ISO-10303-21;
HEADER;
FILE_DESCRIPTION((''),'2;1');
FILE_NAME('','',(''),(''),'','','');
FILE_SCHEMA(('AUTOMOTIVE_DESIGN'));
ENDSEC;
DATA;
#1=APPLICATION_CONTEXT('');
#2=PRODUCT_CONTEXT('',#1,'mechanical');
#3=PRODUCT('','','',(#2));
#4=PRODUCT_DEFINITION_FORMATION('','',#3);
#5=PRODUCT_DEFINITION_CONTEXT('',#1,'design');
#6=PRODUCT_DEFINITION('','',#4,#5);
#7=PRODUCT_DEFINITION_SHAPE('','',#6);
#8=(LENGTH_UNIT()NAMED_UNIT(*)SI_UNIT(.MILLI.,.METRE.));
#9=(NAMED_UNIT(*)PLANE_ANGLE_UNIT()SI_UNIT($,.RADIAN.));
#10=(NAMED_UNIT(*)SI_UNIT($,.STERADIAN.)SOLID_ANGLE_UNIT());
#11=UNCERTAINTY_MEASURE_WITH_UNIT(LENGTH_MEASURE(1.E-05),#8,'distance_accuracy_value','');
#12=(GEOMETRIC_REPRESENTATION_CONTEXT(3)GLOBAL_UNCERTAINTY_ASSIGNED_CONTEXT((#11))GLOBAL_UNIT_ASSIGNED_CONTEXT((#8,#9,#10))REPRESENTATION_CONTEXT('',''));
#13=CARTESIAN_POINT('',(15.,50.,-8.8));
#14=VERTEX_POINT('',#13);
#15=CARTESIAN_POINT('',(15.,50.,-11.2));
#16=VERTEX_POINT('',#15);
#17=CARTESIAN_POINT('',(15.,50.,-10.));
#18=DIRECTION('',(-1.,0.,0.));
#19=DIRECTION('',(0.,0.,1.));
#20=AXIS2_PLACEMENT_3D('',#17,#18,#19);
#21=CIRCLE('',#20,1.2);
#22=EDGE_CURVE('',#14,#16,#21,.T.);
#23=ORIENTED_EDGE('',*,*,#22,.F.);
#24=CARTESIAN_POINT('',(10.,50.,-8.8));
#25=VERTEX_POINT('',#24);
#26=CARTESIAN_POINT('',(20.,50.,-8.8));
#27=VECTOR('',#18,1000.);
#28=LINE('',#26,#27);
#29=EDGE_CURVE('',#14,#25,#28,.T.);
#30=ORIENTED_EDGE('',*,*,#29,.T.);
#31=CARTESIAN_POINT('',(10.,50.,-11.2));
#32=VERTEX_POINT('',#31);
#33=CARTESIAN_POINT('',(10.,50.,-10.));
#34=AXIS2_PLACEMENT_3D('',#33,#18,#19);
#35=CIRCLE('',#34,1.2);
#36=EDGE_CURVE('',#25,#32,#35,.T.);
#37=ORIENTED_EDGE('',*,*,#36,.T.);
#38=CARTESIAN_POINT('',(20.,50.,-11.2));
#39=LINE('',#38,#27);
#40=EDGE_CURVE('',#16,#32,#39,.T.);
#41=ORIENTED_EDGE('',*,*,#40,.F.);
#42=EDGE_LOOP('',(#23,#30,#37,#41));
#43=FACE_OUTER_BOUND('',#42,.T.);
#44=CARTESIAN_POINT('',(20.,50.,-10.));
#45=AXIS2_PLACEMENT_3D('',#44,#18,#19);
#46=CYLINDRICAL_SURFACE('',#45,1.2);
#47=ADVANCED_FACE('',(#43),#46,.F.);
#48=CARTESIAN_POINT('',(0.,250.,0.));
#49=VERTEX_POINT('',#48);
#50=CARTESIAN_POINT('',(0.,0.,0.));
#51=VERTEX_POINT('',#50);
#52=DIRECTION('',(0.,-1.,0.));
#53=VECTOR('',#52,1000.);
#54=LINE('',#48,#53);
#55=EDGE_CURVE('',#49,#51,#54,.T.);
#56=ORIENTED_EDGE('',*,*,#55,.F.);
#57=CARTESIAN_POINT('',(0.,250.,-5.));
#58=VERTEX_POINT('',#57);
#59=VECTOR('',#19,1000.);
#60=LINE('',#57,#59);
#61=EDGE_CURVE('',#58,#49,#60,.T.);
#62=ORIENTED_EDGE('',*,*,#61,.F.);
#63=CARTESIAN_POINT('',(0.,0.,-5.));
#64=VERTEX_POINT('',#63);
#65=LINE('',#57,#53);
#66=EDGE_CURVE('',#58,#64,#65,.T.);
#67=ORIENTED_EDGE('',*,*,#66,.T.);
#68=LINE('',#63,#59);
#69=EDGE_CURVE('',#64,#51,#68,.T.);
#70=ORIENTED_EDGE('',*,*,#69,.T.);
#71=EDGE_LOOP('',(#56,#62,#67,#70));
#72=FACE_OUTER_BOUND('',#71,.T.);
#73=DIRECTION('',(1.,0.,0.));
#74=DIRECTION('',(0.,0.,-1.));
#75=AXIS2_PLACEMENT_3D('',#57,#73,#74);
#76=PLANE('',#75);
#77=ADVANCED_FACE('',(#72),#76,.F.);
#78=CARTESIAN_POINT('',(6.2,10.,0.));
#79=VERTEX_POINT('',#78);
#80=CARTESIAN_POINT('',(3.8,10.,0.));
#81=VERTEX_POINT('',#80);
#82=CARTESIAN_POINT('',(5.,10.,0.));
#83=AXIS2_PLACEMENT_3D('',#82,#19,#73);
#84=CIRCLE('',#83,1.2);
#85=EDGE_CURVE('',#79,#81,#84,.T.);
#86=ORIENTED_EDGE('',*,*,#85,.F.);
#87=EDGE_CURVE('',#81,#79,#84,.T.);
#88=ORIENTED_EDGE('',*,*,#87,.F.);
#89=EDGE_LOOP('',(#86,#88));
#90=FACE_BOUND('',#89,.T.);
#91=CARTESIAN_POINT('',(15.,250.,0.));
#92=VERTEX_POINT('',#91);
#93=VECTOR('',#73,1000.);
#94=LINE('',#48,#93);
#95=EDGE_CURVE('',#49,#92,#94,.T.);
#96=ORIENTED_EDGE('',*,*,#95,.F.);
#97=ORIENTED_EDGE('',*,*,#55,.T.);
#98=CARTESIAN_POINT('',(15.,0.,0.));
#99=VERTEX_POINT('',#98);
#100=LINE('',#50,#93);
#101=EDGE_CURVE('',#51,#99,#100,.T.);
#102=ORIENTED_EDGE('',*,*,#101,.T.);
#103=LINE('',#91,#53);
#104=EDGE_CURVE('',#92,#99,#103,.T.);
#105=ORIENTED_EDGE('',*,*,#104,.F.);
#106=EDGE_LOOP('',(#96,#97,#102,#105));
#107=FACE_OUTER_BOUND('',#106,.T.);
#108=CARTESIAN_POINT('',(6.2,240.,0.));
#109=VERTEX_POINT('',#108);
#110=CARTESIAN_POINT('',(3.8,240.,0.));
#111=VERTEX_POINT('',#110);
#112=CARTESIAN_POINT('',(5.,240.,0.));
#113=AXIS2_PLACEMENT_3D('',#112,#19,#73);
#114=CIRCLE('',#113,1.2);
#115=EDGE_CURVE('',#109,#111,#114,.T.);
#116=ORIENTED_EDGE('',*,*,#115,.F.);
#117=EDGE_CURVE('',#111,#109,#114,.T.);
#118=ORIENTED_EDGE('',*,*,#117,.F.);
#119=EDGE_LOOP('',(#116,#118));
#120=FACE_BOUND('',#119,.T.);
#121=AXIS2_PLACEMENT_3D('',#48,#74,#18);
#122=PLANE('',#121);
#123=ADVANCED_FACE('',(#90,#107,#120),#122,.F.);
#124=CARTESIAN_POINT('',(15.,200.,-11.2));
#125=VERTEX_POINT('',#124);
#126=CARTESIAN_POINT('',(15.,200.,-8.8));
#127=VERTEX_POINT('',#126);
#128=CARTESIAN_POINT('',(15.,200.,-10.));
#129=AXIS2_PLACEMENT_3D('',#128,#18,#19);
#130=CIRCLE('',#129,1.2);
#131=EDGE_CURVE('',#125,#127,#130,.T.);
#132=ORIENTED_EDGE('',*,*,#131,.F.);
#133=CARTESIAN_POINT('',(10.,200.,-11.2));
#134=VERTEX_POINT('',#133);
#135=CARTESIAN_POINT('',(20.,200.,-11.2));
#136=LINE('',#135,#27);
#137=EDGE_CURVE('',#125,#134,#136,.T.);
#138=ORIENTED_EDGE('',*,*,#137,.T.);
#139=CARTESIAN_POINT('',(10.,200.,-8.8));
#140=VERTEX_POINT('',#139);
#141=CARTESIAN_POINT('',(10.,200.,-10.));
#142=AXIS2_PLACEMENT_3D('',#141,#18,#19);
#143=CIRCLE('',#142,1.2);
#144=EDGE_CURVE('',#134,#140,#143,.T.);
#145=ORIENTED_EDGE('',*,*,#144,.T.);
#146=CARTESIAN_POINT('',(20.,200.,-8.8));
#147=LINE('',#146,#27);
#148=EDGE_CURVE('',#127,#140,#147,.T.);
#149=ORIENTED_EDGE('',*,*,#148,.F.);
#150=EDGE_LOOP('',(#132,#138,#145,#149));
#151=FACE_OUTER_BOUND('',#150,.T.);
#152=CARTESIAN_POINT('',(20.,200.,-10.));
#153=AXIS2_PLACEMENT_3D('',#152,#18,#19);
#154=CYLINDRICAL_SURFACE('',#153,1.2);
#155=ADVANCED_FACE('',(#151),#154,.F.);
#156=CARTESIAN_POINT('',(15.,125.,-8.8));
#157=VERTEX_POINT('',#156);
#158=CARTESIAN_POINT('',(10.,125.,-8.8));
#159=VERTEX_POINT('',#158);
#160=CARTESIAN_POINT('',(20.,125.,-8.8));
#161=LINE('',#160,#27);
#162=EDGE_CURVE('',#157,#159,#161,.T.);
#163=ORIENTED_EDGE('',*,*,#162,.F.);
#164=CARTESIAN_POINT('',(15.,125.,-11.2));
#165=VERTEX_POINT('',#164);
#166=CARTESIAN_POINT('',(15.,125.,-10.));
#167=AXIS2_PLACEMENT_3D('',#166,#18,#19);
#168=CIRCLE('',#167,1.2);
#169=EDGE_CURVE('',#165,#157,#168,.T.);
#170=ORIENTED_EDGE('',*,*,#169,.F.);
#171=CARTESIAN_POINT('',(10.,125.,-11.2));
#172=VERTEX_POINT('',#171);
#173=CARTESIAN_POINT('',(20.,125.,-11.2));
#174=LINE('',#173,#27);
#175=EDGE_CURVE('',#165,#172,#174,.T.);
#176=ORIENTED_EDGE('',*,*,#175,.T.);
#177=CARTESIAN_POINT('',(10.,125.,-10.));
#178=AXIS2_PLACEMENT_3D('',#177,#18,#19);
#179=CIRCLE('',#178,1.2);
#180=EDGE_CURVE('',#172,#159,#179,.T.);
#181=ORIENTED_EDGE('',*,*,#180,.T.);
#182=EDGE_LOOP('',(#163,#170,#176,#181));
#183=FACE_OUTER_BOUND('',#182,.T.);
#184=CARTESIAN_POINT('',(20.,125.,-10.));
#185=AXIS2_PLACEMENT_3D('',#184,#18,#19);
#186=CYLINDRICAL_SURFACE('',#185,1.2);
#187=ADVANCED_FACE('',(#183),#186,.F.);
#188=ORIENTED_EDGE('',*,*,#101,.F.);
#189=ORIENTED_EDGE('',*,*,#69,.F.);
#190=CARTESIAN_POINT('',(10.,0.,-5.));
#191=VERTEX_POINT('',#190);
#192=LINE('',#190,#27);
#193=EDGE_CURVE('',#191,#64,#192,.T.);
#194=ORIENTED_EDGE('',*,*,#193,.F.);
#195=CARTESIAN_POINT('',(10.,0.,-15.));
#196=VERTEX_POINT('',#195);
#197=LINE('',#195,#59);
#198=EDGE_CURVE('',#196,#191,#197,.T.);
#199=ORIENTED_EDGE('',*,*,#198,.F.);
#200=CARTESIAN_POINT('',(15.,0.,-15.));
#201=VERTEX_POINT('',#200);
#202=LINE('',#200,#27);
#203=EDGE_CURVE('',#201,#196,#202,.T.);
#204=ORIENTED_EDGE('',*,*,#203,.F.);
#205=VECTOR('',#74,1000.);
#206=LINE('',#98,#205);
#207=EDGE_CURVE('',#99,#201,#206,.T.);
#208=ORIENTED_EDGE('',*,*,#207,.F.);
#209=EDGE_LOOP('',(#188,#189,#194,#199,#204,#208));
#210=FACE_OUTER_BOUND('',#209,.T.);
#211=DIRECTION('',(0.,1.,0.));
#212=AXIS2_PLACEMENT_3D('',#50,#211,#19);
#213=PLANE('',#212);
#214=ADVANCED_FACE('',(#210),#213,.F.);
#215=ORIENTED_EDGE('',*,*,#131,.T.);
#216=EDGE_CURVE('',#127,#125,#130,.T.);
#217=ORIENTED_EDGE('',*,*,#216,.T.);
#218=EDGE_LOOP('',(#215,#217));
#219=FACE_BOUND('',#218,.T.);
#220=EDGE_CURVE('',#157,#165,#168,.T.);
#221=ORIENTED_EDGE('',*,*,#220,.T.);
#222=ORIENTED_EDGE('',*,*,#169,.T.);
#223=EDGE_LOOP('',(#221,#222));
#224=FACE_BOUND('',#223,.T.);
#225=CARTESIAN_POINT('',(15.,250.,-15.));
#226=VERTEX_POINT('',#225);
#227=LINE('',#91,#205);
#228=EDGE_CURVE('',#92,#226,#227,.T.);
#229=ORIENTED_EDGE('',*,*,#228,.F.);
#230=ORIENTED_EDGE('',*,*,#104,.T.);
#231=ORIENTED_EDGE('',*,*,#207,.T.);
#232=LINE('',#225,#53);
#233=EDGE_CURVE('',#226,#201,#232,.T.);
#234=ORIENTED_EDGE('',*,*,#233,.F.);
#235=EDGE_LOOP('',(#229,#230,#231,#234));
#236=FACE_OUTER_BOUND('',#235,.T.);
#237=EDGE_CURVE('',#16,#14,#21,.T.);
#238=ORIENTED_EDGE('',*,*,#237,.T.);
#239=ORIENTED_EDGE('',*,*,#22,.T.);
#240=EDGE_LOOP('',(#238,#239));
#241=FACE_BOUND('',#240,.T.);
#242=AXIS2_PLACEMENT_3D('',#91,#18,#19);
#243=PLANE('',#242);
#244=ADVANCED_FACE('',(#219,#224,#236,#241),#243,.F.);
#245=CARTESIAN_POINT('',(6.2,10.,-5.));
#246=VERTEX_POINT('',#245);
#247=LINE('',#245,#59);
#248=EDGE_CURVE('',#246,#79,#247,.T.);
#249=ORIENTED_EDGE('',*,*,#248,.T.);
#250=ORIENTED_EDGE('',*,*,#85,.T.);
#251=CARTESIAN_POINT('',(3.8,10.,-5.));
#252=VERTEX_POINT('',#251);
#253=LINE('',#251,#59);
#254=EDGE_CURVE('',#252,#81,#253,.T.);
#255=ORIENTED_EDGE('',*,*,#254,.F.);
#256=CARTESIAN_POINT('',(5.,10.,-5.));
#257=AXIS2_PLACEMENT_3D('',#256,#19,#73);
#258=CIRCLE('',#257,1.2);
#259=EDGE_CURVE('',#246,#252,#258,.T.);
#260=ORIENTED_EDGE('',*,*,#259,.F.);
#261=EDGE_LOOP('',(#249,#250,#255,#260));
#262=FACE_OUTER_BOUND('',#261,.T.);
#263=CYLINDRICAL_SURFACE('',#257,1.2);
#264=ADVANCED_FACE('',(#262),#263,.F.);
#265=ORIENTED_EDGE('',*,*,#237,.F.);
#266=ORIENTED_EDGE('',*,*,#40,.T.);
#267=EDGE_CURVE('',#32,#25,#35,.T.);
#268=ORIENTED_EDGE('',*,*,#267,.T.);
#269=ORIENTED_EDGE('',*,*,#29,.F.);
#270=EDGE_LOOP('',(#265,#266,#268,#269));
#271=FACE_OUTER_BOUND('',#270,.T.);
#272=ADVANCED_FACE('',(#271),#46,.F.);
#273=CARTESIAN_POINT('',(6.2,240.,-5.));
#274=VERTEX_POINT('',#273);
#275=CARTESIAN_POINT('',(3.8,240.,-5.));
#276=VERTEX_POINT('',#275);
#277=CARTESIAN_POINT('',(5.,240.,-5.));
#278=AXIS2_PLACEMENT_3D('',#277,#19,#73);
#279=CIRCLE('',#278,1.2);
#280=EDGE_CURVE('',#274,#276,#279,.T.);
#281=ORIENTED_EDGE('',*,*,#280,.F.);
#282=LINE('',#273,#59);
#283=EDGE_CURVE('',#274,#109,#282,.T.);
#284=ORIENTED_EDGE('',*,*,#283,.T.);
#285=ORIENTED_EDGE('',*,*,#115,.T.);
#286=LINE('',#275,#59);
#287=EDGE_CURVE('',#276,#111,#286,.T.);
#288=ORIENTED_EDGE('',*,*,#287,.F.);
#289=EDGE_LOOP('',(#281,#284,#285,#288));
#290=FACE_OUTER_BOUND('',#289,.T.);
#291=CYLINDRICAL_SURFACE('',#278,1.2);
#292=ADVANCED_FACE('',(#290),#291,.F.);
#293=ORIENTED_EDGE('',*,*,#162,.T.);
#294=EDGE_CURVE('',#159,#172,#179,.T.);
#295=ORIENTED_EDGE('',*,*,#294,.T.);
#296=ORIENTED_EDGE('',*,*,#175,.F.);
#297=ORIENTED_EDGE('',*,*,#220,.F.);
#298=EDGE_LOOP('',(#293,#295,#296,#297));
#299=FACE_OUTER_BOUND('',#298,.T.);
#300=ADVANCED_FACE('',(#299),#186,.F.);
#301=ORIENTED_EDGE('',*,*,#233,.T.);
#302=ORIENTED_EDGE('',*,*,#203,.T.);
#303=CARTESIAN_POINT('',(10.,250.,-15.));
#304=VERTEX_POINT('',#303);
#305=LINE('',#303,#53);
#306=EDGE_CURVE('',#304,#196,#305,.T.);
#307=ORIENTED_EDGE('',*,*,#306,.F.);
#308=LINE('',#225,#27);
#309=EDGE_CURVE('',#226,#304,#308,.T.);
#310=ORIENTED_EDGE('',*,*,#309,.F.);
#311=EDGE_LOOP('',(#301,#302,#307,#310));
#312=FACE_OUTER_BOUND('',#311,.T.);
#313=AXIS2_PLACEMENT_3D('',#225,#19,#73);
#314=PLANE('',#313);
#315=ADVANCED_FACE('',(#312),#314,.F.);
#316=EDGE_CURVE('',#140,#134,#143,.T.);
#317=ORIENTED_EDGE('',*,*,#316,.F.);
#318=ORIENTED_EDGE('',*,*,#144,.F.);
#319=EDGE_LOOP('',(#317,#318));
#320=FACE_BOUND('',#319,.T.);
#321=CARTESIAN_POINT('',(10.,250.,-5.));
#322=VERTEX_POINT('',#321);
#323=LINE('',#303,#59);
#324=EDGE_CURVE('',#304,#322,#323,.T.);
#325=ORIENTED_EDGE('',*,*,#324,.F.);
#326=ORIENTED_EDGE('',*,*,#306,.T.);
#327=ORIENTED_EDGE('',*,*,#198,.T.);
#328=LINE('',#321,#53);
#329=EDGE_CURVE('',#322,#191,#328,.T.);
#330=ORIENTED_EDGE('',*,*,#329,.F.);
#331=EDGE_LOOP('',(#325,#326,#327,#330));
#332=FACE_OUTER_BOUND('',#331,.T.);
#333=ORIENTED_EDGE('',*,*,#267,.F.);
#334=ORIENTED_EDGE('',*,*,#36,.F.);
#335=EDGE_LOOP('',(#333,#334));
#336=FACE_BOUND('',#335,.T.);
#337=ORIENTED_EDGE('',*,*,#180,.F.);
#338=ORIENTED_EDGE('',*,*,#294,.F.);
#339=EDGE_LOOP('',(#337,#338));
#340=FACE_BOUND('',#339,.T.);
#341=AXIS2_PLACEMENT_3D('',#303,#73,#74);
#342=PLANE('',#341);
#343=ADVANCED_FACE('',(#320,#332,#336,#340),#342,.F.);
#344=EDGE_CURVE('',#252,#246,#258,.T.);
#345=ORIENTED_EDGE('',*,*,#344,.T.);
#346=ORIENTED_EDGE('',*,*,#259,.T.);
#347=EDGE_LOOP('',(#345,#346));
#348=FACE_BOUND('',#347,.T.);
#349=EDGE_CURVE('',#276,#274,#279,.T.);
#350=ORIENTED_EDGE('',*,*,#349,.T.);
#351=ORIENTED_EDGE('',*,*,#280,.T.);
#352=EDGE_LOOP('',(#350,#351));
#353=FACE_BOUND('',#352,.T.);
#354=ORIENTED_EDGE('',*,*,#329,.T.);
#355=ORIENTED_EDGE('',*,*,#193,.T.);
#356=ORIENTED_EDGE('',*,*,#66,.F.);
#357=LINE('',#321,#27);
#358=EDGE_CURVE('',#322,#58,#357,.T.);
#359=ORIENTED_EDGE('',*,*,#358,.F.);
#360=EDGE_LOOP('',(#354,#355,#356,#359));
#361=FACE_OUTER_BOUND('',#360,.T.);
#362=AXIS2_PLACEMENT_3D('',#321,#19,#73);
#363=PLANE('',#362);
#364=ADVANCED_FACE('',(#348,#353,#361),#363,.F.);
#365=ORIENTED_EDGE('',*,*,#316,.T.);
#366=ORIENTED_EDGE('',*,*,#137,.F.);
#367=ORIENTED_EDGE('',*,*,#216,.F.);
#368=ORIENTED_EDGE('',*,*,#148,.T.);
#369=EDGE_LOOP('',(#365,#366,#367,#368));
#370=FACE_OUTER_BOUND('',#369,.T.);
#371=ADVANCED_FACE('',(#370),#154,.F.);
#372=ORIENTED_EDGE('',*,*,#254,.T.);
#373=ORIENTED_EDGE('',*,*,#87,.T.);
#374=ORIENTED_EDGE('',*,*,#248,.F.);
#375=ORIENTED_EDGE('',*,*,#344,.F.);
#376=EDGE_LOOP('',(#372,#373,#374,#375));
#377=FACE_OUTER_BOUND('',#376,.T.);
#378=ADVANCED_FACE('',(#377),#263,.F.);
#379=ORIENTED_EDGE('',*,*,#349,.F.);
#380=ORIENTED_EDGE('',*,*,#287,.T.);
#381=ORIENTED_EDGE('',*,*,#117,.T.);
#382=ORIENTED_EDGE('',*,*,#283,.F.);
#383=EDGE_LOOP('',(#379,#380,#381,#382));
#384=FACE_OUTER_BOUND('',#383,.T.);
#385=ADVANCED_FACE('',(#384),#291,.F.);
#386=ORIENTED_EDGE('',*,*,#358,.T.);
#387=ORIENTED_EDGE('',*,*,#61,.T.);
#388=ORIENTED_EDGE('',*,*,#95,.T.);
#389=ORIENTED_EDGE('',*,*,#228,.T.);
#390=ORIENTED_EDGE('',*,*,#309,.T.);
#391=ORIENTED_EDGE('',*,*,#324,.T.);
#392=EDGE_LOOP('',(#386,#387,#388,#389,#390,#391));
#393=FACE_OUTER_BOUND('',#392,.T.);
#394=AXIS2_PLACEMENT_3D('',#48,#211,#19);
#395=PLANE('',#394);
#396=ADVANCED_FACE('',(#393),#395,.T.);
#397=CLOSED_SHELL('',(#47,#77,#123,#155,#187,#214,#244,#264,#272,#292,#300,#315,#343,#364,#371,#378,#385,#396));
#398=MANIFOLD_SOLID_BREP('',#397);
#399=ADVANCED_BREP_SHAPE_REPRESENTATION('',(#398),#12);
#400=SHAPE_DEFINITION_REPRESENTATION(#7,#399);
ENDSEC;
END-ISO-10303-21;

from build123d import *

# Parameters (mm, degrees)
BOSS_EXTRUDE1_DEPTH = 250
SKETCH3_R           = 1.2
CUT_EXTRUDE1_DEPTH  = 10
SKETCH4_R           = 1.2
CUT_EXTRUDE2_DEPTH  = 5


with BuildPart() as part:
    # Sketch1 → Boss-Extrude1 (new body)
    with BuildSketch(Plane(origin=(0, 0, 0), x_dir=(1, 0, 0), z_dir=(0, 1, 0))):
        Polygon((0, 0), (15, 0), (15, 15), (10, 15), (10, 5), (0, 5), align=None)
    extrude(amount=BOSS_EXTRUDE1_DEPTH)

    # Sketch3 → Cut-Extrude1 (cut)
    with BuildSketch(Plane.ZY.offset(-10)):
        with Locations((-10, 50)):
            Circle(SKETCH3_R)
        with Locations((-10, 125)):
            Circle(SKETCH3_R)
        with Locations((-10, 200)):
            Circle(SKETCH3_R)
    extrude(amount=-CUT_EXTRUDE1_DEPTH, mode=Mode.SUBTRACT)

    # Sketch4 → Cut-Extrude2 (cut)
    with BuildSketch(Plane.XY):
        with Locations((5, 10)):
            Circle(SKETCH4_R)
        with Locations((5, 240)):
            Circle(SKETCH4_R)
    extrude(amount=-CUT_EXTRUDE2_DEPTH, mode=Mode.SUBTRACT)


solid = part.part
